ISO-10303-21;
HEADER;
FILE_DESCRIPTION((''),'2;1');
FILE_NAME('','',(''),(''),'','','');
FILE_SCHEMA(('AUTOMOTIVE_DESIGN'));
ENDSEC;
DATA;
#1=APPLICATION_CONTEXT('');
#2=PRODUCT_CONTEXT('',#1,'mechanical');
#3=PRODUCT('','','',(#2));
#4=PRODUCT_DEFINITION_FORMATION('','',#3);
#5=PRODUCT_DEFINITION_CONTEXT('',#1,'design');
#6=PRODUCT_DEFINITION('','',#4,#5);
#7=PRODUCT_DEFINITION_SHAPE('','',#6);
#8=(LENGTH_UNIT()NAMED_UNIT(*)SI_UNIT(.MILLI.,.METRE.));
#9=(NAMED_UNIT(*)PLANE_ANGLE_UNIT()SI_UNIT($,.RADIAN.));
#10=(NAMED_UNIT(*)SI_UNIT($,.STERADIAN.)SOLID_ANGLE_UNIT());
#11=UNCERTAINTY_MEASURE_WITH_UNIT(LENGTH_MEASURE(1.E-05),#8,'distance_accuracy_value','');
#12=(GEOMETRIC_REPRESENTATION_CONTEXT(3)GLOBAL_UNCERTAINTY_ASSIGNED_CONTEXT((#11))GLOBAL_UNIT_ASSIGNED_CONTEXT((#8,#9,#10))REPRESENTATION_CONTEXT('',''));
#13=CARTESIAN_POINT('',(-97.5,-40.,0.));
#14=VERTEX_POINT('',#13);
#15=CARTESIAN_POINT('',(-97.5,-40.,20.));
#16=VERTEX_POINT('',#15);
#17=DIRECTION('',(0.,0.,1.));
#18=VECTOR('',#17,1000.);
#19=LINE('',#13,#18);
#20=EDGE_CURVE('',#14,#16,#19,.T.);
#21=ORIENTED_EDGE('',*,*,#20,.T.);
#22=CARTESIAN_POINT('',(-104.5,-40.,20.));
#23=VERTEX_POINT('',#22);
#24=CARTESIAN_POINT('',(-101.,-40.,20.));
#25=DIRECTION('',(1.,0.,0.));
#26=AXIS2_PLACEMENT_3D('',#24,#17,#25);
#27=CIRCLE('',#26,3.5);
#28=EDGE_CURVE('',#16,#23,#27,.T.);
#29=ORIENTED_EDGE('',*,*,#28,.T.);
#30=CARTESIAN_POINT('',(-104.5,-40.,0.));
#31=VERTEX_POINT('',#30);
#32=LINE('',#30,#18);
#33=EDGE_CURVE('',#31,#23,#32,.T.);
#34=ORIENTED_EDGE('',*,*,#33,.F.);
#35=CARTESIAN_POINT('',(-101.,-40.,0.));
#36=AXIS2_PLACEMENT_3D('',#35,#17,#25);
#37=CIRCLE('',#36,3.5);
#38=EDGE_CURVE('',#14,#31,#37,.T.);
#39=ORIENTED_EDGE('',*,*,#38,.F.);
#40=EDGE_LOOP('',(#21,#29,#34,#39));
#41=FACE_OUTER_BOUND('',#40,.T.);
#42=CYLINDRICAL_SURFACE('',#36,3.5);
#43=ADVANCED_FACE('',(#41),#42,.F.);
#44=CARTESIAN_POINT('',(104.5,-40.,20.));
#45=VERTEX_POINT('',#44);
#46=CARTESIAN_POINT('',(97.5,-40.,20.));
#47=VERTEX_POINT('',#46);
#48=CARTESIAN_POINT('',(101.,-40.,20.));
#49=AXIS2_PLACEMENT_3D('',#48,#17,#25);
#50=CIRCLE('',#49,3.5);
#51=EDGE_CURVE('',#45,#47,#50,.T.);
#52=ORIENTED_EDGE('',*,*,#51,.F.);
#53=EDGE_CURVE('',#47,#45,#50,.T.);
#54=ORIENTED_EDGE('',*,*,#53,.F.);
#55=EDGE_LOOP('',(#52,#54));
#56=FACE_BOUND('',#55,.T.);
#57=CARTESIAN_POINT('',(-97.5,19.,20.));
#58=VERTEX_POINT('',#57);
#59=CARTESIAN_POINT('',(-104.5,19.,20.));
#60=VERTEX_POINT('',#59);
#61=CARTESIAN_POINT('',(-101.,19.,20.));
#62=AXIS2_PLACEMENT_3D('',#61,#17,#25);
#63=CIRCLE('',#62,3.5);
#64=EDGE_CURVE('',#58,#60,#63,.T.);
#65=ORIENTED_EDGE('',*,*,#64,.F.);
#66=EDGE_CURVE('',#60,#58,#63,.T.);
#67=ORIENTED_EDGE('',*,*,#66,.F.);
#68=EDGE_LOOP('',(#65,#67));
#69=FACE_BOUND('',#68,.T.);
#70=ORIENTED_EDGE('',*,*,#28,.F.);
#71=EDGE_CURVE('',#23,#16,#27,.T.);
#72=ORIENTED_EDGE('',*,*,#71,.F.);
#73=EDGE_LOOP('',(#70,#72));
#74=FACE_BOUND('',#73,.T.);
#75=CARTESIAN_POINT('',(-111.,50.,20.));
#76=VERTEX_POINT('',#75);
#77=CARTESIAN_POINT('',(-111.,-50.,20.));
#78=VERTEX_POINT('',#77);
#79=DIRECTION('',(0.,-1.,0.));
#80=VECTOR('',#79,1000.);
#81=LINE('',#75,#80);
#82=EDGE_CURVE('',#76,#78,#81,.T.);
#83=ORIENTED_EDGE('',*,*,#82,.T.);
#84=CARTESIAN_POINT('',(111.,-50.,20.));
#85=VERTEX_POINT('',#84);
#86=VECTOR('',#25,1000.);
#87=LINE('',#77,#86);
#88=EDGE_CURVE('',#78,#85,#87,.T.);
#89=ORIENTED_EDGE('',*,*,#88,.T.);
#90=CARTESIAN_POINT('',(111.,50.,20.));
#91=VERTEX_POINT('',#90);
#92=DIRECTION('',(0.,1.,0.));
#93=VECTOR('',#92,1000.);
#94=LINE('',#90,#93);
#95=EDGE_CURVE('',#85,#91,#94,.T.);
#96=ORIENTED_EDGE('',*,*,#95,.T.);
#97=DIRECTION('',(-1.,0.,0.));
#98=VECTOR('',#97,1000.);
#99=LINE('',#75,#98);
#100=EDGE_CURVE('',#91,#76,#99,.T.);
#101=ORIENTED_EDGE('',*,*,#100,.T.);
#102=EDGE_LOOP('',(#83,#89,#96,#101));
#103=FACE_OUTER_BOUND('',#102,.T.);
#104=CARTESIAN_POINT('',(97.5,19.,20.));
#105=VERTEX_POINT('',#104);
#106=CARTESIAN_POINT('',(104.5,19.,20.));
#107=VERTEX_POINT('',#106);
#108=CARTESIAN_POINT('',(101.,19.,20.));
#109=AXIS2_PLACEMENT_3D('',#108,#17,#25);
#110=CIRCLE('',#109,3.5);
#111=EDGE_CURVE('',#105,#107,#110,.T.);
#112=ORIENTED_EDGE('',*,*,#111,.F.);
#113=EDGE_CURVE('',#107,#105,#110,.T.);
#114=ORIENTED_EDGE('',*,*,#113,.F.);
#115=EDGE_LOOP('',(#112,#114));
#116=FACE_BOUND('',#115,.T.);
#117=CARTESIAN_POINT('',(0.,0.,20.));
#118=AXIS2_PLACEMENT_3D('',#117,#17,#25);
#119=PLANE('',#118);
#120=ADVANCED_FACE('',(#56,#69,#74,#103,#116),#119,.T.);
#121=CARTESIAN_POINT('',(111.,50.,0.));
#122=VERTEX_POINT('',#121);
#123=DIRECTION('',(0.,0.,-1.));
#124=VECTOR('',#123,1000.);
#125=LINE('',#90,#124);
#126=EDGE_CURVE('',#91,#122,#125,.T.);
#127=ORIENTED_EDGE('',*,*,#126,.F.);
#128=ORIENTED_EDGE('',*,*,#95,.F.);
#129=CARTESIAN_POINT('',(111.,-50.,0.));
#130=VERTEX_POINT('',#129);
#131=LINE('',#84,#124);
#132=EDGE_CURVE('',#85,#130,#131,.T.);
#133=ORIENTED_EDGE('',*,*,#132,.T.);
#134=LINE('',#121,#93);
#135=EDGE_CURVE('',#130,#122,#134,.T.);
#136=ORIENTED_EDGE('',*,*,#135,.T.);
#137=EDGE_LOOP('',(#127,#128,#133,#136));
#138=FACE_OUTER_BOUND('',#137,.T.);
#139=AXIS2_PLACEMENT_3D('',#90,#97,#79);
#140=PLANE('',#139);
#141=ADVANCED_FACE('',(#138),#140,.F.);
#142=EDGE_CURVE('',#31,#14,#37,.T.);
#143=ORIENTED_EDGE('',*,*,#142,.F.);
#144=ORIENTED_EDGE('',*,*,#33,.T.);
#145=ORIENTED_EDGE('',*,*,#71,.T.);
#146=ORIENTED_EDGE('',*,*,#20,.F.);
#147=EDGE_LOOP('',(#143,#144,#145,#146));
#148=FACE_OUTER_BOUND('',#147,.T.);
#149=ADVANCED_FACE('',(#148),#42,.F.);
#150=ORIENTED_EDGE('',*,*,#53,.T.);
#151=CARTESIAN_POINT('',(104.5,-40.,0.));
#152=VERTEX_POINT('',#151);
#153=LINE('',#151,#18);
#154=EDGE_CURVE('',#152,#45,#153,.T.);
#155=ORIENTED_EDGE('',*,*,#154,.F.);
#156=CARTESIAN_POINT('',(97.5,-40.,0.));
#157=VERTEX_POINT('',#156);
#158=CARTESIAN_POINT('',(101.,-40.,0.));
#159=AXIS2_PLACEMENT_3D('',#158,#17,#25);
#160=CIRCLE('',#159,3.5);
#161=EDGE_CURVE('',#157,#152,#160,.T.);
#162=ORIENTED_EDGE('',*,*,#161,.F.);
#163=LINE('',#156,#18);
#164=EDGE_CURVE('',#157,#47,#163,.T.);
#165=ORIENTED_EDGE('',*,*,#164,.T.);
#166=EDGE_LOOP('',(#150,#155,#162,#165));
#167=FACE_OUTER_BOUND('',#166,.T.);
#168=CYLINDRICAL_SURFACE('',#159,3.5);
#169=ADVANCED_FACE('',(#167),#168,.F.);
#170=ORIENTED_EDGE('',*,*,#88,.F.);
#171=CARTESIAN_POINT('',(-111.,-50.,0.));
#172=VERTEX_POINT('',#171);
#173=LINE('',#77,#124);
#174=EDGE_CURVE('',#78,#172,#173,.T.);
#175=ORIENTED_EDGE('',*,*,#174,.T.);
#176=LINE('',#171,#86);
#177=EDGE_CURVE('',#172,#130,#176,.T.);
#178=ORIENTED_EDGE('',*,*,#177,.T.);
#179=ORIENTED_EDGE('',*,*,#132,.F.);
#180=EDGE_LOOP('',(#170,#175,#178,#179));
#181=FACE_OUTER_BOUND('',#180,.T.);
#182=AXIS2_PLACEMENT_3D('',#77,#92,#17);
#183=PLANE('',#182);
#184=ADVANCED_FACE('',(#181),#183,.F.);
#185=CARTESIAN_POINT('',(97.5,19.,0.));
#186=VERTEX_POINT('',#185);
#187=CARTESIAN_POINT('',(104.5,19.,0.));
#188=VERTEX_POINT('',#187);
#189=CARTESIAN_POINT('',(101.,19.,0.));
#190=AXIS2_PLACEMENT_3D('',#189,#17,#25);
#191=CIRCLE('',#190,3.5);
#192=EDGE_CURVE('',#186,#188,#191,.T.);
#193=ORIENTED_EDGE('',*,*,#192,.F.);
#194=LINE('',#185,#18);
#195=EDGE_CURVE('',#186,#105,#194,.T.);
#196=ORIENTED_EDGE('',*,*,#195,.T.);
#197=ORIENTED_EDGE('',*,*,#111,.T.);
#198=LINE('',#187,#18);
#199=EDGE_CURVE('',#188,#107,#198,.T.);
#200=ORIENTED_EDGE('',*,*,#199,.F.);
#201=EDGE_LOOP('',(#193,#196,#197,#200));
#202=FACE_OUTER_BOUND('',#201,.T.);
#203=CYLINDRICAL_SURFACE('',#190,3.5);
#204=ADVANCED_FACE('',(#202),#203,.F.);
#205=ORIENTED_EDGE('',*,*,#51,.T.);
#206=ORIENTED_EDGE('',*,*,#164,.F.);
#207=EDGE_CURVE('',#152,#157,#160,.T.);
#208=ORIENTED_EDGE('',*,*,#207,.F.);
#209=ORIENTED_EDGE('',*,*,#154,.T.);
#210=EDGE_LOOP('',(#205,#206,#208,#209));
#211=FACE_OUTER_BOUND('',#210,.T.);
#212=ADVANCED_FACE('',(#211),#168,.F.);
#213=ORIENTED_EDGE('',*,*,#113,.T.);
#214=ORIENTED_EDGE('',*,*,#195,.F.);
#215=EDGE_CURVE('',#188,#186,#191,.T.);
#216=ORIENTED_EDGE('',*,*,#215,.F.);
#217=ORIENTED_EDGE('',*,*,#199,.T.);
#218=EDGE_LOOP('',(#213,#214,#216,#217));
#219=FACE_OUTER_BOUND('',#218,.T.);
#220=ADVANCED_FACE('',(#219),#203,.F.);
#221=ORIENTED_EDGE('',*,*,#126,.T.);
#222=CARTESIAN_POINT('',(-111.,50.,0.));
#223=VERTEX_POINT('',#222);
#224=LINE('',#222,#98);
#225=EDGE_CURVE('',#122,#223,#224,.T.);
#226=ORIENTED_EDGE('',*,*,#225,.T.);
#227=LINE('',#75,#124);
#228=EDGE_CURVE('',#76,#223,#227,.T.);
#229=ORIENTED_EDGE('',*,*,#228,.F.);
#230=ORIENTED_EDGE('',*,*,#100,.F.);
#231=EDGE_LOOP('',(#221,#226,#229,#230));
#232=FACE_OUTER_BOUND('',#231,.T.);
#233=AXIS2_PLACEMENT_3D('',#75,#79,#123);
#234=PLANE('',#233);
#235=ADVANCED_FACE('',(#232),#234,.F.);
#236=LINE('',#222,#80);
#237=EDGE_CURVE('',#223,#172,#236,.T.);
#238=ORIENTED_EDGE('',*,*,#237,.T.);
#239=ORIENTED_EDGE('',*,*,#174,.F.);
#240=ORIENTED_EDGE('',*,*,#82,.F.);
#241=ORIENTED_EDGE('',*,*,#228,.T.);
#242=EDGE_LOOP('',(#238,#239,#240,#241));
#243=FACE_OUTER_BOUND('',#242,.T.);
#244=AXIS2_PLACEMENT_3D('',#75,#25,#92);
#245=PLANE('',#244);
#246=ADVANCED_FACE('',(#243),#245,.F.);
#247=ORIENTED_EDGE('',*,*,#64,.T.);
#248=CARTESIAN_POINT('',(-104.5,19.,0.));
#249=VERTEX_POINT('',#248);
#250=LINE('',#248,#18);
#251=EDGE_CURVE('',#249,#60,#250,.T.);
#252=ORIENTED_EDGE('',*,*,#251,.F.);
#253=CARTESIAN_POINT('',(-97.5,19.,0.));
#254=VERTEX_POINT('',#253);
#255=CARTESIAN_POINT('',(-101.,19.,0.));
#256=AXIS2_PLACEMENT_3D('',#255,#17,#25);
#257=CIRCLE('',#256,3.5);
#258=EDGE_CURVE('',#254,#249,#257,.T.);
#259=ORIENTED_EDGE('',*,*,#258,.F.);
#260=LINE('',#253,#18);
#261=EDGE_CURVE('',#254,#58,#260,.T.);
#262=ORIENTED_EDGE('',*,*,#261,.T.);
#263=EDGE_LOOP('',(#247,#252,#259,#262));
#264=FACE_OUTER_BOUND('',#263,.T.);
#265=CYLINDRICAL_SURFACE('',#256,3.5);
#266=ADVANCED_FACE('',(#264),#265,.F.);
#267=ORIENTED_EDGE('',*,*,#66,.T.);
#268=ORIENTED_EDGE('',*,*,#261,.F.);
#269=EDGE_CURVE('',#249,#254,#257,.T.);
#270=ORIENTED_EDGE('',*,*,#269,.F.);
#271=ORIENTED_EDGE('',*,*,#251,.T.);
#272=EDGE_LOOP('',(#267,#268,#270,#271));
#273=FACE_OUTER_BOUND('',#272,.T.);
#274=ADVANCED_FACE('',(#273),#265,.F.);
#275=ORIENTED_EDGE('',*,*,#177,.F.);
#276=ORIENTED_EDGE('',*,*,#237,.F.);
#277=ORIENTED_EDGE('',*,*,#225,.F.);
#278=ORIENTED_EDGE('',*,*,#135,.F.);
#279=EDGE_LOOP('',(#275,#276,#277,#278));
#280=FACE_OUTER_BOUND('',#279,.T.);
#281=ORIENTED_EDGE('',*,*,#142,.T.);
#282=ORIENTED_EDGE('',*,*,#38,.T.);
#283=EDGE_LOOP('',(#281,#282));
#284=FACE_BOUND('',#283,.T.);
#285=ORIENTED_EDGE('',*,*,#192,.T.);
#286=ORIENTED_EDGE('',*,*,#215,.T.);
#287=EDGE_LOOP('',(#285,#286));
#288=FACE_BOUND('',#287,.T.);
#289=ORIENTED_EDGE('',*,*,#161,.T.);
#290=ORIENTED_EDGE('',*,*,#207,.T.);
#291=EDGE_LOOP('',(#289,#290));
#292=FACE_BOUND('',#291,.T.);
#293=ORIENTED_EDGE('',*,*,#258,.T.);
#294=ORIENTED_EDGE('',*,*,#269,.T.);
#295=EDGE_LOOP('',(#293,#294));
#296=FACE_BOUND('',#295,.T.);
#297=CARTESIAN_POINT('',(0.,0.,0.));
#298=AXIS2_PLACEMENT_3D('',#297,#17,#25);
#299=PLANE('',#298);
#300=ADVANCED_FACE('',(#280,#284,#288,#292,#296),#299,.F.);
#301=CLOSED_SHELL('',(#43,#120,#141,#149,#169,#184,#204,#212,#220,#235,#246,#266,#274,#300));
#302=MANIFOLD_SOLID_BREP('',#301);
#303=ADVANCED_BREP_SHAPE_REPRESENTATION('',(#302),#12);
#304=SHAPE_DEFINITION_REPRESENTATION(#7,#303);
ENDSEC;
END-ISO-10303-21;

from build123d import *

# Parameters (mm, degrees)
SKETCH_1_W          = 222
SKETCH_1_H          = 100
EXTRUDE_1_DEPTH     = 20
SKETCH_4_R          = 3.5
CUT_EXTRUDE_1_DEPTH = 124.37341691


with BuildPart() as part:
    # 草图1 → 凸台-拉伸1 (new body)
    with BuildSketch(Plane.XY):
        Rectangle(SKETCH_1_W, SKETCH_1_H)
    extrude(amount=EXTRUDE_1_DEPTH)

    # 草图4 → 切除-拉伸1 (cut, through all)
    with BuildSketch(Plane.XY.offset(20)):
        with Locations((-101, 19)):
            Circle(SKETCH_4_R)
        with Locations((-101, -40)):
            Circle(SKETCH_4_R)
        with Locations((101, 19)):
            Circle(SKETCH_4_R)
        with Locations((101, -40)):
            Circle(SKETCH_4_R)
    extrude(amount=-CUT_EXTRUDE_1_DEPTH, mode=Mode.SUBTRACT)


solid = part.part
